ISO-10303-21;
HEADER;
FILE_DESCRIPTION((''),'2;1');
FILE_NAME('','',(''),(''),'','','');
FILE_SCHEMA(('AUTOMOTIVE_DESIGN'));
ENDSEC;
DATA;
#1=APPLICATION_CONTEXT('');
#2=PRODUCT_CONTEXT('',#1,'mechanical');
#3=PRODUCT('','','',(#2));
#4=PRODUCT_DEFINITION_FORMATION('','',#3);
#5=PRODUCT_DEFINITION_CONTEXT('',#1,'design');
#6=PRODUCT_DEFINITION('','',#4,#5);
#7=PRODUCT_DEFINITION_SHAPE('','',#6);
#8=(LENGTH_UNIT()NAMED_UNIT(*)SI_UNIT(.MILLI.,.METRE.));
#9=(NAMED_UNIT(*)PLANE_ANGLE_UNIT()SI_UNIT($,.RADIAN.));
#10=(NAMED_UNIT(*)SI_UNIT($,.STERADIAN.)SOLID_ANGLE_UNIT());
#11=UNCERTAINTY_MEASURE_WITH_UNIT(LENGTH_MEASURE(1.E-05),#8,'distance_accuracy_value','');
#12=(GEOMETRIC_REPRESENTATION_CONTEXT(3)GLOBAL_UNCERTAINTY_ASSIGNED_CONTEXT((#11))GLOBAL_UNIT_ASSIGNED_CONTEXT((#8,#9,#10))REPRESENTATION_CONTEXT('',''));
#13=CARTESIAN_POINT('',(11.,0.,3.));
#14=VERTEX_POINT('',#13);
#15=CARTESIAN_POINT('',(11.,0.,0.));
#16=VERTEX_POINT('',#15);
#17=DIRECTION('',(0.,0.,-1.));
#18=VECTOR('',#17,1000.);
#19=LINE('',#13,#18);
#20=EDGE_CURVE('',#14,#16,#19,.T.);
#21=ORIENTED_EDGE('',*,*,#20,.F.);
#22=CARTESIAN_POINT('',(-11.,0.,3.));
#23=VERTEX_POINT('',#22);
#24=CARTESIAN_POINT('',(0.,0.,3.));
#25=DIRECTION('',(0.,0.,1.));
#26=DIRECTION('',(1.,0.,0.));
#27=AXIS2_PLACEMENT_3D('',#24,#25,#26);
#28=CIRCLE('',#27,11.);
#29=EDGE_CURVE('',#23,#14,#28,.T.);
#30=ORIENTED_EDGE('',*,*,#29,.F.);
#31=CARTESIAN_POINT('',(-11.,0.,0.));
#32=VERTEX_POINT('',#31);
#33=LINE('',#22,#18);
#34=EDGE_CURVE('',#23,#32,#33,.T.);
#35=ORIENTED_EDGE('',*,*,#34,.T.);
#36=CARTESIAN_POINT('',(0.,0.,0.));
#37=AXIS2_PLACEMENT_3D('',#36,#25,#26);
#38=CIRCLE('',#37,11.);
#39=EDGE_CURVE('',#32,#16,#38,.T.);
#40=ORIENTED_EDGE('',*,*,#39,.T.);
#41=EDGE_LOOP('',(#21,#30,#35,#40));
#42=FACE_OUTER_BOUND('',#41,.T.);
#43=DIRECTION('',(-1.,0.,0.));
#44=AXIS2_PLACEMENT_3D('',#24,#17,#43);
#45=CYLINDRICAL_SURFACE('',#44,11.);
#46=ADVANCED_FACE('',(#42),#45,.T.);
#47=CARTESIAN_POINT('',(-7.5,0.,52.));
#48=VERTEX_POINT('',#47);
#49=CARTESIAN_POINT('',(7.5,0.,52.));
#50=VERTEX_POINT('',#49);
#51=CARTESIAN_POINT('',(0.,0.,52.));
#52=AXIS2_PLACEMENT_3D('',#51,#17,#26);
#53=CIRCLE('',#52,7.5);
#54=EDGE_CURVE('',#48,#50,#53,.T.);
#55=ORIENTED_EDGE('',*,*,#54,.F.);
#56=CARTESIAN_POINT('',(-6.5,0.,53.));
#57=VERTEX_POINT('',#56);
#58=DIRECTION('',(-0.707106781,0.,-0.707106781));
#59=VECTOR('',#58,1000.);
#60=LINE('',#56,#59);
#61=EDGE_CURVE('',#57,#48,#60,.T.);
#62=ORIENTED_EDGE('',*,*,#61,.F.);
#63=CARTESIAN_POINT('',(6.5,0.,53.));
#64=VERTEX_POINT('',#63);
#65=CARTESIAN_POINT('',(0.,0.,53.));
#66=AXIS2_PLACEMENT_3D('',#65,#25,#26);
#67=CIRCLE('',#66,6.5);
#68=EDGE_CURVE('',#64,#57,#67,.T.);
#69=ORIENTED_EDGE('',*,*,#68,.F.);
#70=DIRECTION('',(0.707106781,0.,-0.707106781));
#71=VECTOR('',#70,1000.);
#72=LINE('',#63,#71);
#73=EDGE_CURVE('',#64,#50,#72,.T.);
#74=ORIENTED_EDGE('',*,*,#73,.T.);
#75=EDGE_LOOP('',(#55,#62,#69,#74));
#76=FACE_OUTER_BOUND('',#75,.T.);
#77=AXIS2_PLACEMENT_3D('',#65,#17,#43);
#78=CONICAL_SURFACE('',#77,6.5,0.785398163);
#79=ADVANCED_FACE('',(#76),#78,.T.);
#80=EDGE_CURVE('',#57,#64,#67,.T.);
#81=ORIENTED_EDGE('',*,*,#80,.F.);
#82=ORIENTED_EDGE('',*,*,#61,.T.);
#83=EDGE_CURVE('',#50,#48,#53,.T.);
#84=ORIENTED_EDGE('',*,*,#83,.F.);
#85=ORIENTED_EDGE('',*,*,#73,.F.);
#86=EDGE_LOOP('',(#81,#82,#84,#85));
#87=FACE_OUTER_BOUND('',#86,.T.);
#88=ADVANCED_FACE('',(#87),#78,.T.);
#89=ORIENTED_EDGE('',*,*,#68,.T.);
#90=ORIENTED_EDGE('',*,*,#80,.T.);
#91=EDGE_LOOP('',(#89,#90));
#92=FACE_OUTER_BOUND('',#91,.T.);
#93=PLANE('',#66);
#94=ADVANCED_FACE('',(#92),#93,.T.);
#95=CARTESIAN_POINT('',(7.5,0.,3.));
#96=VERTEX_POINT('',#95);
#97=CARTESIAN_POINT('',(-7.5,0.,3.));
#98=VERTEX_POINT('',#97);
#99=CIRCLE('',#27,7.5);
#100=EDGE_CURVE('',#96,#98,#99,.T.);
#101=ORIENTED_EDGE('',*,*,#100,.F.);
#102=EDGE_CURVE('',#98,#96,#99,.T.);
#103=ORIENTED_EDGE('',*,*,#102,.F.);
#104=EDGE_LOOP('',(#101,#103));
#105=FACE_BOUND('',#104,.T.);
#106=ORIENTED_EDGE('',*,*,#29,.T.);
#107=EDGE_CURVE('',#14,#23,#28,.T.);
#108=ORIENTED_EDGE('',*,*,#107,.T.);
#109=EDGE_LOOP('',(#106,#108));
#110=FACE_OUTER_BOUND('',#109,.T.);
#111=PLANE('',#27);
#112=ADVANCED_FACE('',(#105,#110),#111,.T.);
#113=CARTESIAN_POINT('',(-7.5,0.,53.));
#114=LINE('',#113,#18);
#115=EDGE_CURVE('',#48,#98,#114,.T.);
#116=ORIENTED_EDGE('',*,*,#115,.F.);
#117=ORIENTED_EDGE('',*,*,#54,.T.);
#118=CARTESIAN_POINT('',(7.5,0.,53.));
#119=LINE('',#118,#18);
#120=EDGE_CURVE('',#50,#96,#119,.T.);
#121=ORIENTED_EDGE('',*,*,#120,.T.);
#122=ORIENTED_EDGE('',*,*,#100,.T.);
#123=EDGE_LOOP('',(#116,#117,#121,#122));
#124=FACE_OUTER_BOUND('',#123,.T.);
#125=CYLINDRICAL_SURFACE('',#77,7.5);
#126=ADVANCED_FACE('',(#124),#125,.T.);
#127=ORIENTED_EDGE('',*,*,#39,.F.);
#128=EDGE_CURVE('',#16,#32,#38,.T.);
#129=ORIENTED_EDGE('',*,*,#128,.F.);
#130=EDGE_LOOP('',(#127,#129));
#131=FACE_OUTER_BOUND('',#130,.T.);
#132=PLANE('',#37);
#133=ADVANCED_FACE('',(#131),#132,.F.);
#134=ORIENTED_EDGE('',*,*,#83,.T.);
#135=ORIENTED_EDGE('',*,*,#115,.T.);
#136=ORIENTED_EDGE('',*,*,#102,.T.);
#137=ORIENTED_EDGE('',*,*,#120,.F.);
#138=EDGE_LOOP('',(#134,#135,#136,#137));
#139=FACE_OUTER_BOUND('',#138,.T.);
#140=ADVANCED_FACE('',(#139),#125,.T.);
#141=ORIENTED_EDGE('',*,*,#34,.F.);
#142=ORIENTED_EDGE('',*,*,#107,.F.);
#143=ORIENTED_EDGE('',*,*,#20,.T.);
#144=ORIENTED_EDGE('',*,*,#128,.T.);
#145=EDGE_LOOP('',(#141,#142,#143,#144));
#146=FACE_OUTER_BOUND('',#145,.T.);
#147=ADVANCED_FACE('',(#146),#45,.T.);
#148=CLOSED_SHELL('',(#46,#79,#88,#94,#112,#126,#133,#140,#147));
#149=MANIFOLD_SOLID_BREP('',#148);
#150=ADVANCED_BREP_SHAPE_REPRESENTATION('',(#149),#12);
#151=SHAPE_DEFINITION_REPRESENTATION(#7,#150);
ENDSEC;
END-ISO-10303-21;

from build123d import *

# Parameters (mm, degrees)
SKETCH_1_R      = 11
EXTRUDE_1_DEPTH = 3
SKETCH_2_R      = 7.5
EXTRUDE_2_DEPTH = 50
CHAMFER_1_SIZE  = 1


with BuildPart() as part:
    # 草图1 → 凸台-拉伸1 (new body)
    with BuildSketch(Plane.XY):
        Circle(SKETCH_1_R)
    extrude(amount=EXTRUDE_1_DEPTH)

    # 草图2 → 凸台-拉伸2 (add)
    with BuildSketch(Plane.XY.offset(3)):
        Circle(SKETCH_2_R)
    extrude(amount=EXTRUDE_2_DEPTH)

    # 倒角1
    chamfer_1_edges = [part.edges().sort_by_distance(p)[0] for p in [
        (-7.5, 0, 53),
    ]]
    chamfer(chamfer_1_edges, length=CHAMFER_1_SIZE)


solid = part.part
